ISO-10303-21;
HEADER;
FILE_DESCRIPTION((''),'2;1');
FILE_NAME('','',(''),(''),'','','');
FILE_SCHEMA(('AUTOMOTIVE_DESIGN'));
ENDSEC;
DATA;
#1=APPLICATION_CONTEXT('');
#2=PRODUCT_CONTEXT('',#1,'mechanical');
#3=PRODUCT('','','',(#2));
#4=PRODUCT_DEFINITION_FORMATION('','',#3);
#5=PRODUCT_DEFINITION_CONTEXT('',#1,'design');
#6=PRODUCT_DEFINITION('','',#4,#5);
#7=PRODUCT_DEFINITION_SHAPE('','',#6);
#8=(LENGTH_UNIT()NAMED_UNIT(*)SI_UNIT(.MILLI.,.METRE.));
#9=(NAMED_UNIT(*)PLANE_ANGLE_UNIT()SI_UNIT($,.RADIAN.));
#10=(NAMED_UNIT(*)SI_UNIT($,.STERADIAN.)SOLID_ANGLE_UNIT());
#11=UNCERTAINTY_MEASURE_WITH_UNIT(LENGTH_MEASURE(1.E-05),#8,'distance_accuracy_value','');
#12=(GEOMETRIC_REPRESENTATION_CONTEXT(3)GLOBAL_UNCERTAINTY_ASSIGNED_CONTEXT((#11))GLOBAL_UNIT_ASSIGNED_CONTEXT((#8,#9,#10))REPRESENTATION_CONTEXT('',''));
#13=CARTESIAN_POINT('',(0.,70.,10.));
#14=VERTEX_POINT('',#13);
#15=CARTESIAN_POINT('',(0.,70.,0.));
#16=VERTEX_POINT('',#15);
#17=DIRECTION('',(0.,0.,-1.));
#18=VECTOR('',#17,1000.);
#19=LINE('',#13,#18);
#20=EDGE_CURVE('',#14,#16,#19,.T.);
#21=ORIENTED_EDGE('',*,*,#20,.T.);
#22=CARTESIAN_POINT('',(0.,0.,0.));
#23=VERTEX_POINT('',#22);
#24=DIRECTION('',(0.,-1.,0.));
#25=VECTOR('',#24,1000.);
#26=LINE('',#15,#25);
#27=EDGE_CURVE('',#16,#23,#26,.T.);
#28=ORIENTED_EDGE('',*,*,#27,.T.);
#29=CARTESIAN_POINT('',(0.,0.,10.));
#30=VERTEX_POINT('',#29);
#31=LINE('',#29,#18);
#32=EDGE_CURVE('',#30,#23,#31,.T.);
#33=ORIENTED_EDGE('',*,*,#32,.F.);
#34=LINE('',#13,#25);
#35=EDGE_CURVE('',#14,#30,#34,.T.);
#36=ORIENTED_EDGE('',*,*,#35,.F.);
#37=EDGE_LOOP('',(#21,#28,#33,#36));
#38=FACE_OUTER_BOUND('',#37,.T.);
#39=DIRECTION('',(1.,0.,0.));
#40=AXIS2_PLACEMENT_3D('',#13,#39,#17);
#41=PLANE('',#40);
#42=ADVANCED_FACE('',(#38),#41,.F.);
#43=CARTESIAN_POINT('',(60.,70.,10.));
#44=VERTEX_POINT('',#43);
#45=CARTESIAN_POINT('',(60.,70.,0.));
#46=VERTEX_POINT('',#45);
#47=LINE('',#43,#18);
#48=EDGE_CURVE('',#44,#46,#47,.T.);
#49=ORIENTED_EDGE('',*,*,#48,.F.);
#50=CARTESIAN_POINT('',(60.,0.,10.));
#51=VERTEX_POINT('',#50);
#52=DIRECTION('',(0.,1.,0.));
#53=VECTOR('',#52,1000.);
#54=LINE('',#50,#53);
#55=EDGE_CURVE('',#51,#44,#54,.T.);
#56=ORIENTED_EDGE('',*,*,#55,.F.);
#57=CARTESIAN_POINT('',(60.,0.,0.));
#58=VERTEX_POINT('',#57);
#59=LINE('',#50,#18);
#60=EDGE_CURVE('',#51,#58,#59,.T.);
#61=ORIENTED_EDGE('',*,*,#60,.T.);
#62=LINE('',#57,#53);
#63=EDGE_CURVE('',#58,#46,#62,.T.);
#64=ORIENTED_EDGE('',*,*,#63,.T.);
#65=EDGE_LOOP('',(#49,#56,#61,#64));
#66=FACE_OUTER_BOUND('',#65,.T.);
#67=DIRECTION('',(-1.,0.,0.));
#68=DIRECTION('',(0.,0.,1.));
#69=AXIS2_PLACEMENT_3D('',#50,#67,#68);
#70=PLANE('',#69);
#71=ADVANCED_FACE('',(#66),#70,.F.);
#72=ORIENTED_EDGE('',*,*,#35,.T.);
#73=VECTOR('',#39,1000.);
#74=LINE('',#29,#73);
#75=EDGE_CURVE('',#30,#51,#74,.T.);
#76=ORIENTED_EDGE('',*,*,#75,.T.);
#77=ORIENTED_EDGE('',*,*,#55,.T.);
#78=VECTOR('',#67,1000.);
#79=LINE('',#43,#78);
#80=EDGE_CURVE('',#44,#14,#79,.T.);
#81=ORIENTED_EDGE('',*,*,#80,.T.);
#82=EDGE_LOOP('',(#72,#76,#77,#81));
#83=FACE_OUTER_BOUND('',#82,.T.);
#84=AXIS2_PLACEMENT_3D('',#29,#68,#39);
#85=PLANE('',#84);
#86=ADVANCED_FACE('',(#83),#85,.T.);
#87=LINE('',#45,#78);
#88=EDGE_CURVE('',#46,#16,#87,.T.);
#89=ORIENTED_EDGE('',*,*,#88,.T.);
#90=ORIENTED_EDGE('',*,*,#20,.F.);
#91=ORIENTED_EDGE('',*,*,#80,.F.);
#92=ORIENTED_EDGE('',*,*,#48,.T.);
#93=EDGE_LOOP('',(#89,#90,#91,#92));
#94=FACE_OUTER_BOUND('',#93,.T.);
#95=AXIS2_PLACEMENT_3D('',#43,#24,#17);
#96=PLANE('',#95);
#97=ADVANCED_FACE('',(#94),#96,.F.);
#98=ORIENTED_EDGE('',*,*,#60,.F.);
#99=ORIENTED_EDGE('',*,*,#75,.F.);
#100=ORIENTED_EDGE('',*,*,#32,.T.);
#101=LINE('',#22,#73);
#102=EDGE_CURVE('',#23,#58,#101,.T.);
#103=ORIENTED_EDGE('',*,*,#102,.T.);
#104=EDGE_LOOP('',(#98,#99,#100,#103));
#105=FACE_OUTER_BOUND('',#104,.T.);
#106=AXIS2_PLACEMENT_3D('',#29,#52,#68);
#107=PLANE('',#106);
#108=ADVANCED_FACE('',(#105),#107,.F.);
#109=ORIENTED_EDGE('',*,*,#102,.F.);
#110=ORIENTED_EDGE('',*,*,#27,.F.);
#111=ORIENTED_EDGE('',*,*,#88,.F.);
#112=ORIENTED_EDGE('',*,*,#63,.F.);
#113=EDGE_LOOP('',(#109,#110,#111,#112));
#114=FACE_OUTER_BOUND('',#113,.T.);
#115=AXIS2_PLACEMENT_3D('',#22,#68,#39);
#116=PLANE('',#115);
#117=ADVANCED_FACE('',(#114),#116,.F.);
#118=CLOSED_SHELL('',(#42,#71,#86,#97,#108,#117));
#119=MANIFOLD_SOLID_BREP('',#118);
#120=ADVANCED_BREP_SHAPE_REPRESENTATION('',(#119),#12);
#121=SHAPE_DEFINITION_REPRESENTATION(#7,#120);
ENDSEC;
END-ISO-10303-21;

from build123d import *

# Parameters (mm, degrees)
SKETCH_1_W      = 60
SKETCH_1_H      = 70
EXTRUDE_1_DEPTH = 10


with BuildPart() as part:
    # 草图1 → 凸台-拉伸1 (new body)
    with BuildSketch(Plane.XY):
        with Locations((30, 35)):
            Rectangle(SKETCH_1_W, SKETCH_1_H)
    extrude(amount=EXTRUDE_1_DEPTH)


solid = part.part
